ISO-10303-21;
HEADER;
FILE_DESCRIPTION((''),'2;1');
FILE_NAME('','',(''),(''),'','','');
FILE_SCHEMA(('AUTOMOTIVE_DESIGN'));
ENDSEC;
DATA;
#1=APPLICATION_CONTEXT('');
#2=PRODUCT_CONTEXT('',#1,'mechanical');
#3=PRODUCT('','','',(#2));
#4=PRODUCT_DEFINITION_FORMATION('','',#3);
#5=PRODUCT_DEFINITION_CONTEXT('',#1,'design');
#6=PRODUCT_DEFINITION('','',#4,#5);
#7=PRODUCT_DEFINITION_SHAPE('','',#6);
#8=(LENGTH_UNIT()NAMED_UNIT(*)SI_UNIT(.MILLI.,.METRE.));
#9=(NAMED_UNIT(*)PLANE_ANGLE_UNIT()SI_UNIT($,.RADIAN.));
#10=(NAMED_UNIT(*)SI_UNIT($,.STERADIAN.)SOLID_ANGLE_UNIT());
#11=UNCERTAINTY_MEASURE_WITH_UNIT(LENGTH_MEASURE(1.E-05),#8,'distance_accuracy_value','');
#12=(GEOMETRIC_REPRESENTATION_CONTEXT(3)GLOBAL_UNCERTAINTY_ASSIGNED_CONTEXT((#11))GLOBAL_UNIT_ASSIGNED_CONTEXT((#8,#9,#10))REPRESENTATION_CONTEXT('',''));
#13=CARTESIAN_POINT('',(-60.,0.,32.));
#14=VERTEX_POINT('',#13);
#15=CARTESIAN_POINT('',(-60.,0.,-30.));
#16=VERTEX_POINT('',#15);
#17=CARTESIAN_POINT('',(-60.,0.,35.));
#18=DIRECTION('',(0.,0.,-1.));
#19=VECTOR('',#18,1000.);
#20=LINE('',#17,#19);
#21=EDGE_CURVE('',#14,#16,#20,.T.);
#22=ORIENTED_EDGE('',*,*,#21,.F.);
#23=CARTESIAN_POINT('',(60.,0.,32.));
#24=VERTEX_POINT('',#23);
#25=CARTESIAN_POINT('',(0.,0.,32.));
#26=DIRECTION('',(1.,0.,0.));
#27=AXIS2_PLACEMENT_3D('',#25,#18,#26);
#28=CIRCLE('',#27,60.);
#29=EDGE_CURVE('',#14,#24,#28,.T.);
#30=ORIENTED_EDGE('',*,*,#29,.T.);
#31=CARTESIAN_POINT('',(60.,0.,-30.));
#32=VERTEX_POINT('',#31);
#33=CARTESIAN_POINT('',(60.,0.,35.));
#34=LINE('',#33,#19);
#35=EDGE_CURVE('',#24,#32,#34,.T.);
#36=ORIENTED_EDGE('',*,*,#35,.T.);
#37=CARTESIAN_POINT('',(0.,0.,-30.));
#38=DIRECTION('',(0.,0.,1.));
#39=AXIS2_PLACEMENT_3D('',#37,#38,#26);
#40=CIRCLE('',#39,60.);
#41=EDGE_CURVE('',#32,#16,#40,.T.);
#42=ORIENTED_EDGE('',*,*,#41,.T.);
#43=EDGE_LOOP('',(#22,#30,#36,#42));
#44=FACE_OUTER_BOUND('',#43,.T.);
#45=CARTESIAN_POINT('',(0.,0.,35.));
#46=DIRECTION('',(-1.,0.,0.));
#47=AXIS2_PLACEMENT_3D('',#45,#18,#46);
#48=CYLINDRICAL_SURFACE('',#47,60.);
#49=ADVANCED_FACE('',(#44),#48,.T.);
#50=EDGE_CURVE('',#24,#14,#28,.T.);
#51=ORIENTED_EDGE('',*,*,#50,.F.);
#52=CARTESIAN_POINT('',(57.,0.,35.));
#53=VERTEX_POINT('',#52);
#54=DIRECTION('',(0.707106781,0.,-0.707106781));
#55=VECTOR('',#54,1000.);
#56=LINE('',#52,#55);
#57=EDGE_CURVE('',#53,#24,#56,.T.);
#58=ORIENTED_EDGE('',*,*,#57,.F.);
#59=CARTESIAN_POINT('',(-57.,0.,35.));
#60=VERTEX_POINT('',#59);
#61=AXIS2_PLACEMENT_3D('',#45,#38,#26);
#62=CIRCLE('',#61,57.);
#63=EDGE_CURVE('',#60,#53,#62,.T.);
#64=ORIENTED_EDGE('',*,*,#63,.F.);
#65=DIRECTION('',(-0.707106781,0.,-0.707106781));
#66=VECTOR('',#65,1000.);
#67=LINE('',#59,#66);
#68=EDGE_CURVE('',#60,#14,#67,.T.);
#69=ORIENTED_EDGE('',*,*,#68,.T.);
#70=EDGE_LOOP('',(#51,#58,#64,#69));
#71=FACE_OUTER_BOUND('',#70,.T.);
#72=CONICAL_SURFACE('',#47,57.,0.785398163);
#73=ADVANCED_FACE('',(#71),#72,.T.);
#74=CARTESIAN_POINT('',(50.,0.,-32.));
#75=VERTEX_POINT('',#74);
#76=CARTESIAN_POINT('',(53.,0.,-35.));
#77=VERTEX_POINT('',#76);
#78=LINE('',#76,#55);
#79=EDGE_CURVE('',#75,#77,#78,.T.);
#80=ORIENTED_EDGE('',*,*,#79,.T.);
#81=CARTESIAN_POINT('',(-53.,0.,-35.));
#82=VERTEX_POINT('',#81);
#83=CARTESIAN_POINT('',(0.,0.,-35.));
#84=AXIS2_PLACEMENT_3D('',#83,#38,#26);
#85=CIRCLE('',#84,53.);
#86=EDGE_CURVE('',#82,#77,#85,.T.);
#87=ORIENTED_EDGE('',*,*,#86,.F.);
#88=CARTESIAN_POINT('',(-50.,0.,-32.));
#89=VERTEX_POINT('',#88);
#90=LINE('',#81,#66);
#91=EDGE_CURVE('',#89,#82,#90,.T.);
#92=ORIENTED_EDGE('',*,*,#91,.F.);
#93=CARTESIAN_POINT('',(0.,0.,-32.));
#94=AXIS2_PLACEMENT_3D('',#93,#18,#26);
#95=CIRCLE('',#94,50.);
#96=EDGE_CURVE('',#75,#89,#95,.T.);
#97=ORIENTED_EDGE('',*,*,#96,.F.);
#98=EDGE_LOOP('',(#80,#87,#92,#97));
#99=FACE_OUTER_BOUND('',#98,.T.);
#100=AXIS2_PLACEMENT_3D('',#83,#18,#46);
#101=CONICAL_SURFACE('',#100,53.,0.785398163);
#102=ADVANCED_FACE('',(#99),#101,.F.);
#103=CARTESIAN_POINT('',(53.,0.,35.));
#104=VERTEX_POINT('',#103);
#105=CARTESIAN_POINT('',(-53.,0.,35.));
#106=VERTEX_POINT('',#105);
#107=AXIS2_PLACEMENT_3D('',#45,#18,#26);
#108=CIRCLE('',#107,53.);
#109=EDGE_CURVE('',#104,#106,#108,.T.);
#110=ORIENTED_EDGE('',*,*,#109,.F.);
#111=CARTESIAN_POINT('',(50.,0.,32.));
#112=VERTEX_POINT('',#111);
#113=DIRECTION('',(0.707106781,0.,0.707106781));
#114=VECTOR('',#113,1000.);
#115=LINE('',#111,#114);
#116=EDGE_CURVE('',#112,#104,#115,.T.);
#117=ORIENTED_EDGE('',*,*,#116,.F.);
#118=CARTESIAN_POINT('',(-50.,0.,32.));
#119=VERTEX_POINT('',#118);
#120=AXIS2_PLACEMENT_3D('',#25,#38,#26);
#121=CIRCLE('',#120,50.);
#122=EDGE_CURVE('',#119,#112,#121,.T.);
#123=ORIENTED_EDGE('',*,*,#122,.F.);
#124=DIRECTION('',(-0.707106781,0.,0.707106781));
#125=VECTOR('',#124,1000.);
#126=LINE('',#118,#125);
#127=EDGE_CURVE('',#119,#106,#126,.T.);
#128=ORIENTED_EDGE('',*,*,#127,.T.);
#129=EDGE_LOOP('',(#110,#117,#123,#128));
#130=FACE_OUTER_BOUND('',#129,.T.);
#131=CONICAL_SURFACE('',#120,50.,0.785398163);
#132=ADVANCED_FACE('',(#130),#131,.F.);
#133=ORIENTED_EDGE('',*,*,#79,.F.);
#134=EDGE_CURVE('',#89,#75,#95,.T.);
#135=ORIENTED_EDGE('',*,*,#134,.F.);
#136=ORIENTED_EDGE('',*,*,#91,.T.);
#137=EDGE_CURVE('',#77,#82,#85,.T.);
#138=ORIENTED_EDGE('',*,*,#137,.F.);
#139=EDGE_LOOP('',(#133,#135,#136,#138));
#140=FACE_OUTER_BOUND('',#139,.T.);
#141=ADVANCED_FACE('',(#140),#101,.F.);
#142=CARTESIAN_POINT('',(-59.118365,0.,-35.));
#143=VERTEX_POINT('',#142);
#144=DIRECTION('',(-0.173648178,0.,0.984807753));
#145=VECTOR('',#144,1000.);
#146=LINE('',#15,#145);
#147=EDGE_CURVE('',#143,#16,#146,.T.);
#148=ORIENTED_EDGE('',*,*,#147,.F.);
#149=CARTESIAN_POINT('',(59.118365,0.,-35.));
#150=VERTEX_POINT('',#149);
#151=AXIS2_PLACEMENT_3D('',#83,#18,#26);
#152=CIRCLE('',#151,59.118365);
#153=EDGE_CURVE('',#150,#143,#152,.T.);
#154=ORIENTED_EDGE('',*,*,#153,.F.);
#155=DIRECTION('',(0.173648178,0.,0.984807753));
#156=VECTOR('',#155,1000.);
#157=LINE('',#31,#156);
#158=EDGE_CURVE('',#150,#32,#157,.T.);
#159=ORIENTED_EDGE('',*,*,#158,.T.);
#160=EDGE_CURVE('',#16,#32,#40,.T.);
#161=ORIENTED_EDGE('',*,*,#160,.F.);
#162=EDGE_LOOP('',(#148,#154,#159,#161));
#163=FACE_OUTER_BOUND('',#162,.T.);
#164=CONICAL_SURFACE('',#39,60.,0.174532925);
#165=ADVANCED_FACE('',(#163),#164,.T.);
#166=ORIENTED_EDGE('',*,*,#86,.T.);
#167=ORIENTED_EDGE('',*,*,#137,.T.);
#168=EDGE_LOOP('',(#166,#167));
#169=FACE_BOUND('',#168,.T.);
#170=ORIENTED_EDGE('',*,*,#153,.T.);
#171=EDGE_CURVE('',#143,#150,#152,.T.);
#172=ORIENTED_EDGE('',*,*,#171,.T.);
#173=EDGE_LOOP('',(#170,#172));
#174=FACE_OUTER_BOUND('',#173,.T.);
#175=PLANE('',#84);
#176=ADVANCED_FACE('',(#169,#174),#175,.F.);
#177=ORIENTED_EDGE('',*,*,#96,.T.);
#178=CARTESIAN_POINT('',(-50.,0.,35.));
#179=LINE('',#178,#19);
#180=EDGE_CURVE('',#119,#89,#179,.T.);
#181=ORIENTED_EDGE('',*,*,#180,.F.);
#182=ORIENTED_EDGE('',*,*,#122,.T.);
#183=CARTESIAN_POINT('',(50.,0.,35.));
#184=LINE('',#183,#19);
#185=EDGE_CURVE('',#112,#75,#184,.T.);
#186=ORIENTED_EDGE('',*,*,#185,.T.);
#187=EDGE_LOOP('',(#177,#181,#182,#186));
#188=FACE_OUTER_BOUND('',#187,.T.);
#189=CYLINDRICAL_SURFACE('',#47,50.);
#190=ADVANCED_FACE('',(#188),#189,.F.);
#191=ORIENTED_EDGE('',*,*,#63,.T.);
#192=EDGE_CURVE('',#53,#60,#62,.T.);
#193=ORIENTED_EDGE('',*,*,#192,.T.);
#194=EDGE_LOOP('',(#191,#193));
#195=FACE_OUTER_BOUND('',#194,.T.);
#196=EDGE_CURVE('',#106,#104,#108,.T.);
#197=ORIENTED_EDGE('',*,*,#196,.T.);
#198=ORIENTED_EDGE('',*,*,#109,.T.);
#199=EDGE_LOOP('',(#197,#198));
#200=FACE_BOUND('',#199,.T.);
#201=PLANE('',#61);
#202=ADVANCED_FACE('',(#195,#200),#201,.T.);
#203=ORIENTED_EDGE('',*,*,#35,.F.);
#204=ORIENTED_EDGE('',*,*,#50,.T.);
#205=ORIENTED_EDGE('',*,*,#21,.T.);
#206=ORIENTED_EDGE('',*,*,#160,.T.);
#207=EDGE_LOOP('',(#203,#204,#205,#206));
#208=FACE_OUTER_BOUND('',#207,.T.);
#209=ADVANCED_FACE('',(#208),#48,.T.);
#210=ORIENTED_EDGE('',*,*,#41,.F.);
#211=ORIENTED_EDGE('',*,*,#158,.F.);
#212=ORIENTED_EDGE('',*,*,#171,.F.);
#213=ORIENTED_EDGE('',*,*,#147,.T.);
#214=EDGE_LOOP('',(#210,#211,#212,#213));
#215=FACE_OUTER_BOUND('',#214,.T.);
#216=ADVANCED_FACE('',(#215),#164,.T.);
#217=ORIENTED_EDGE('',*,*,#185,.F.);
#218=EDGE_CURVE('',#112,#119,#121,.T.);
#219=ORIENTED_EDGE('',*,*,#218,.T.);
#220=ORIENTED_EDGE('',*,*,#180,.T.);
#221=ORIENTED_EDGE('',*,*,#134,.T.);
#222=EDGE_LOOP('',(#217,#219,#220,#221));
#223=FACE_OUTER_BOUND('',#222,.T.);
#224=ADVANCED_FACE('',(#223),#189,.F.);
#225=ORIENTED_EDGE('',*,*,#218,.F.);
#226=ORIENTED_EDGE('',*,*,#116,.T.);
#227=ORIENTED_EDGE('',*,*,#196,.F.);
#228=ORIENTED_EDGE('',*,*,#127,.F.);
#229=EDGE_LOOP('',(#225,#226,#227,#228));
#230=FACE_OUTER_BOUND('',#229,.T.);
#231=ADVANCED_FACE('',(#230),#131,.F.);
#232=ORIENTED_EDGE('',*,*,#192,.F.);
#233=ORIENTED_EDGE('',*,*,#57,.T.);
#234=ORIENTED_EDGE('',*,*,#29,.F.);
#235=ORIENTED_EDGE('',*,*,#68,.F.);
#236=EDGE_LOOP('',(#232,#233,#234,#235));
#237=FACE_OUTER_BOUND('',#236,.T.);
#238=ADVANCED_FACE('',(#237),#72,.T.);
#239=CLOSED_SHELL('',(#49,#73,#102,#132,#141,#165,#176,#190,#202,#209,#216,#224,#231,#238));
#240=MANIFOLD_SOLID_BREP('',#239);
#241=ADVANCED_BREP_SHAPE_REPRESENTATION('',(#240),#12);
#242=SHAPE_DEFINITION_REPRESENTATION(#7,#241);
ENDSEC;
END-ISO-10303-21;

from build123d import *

# Parameters (mm, degrees)
SKETCH1_R           = 60
SKETCH1_R_2         = 50
BOSS_EXTRUDE1_DEPTH = 35
CHAMFER1_SIZE       = 3
CHAMFER2_SIZE       = 5
CHAMFER2_SIZE2      = 0.881634904


with BuildPart() as part:
    # Sketch1 → Boss-Extrude1 (new, symmetric)
    with BuildSketch(Plane.XY):
        Circle(SKETCH1_R)
        Circle(SKETCH1_R_2, mode=Mode.SUBTRACT)
    extrude(amount=BOSS_EXTRUDE1_DEPTH, both=True)

    # Chamfer1
    chamfer1_edges = [part.edges().sort_by_distance(p)[0] for p in [
        (-60, 0, 35),
        (-50, 0, -35),
        (-50, 0, 35),
    ]]
    chamfer(chamfer1_edges, length=CHAMFER1_SIZE)

    # Chamfer2
    chamfer2_edges = [part.edges().sort_by_distance(p)[0] for p in [
        (-60, 0, -35),
    ]]
    chamfer2_side = [part.faces().sort_by_distance(p)[0] for p in [
        (-60, 0, -1.5),
    ]]
    chamfer(chamfer2_edges, length=CHAMFER2_SIZE, length2=CHAMFER2_SIZE2, reference=chamfer2_side[0])


solid = part.part
